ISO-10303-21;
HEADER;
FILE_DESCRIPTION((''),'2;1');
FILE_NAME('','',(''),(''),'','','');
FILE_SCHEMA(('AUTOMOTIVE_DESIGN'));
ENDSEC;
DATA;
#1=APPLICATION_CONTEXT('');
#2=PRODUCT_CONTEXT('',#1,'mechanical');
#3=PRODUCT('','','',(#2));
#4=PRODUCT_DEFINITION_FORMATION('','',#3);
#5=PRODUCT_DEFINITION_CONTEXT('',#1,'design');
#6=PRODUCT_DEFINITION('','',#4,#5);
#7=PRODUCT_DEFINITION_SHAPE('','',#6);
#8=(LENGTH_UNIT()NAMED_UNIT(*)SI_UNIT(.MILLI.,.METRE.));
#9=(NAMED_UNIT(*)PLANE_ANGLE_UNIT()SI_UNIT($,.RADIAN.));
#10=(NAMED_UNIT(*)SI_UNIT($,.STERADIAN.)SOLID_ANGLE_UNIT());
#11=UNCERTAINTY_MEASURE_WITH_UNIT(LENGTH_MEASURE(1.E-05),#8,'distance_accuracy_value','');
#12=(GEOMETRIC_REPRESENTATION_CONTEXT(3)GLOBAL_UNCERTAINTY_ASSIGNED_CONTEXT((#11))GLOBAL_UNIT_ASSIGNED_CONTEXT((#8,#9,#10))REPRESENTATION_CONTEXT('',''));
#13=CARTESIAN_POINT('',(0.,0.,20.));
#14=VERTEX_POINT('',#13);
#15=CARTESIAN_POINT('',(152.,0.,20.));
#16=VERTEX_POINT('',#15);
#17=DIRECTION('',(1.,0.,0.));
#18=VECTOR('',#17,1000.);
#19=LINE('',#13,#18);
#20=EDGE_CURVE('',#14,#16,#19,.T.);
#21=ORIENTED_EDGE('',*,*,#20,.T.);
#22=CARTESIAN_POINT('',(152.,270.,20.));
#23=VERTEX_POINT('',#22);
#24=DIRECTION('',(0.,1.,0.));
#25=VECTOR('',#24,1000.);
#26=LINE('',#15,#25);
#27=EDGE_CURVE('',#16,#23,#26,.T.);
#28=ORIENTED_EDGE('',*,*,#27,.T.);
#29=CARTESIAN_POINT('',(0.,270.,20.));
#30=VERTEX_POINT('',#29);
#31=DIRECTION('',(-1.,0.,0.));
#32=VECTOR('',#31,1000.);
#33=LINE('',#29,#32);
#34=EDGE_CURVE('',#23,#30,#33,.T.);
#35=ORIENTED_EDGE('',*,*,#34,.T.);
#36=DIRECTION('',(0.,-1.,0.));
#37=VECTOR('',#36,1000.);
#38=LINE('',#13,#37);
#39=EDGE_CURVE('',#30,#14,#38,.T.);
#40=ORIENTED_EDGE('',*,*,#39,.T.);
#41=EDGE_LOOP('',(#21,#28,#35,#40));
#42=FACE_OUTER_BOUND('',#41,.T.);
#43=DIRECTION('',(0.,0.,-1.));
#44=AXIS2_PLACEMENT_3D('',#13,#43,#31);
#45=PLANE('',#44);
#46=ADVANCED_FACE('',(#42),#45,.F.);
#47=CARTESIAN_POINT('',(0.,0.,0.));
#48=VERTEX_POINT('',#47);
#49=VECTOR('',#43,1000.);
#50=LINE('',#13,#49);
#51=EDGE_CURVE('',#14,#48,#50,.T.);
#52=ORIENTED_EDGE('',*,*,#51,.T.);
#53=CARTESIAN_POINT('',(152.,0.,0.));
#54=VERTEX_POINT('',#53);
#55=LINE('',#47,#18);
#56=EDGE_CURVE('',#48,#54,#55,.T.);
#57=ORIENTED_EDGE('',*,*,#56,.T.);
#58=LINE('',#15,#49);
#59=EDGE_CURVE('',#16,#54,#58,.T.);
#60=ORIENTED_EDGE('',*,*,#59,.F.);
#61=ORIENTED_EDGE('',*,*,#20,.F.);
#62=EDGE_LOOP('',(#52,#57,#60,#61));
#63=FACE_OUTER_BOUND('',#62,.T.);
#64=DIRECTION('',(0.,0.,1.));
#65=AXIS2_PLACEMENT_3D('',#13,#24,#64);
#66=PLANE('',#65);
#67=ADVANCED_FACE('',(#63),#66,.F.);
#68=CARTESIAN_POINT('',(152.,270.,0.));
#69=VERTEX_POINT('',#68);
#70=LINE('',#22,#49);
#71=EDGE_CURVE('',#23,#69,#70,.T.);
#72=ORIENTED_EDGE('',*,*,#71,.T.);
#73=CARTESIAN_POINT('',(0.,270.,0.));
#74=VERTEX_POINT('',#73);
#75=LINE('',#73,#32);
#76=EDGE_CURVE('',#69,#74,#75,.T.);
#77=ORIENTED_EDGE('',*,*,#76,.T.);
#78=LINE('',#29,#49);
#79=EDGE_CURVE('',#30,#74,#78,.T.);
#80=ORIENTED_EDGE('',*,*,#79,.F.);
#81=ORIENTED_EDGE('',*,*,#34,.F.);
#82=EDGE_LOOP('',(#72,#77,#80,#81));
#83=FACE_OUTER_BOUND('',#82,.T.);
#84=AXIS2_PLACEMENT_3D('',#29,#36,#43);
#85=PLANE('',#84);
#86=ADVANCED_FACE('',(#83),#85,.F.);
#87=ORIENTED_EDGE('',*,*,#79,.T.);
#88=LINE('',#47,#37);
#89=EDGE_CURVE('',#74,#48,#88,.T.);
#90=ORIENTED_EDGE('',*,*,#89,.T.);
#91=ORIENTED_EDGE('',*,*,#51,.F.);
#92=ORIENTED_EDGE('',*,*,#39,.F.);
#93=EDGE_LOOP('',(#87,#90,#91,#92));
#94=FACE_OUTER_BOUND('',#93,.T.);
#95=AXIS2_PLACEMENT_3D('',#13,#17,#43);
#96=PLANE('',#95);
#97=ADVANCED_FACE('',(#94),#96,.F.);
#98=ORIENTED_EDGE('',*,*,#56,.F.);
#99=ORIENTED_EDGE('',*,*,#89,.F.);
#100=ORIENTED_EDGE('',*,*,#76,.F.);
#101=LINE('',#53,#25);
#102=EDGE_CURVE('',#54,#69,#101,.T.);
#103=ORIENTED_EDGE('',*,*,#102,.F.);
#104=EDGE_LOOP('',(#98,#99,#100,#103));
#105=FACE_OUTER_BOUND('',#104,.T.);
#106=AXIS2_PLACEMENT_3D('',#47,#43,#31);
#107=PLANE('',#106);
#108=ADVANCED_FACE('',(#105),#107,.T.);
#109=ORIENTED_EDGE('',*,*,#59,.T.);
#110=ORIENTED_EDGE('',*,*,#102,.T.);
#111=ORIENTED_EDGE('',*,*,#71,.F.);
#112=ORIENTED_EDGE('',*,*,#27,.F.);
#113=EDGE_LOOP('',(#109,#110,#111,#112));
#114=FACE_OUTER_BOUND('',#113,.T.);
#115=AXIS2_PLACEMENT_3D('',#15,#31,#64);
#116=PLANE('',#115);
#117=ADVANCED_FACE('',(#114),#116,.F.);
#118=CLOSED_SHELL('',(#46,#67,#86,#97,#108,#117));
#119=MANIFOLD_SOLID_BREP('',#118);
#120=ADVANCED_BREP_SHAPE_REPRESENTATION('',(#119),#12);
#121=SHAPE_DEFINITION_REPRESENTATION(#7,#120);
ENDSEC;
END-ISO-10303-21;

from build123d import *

# Parameters (mm, degrees)
SKETCH1_W           = 152
SKETCH1_H           = 270
BOSS_EXTRUDE1_DEPTH = 20


with BuildPart() as part:
    # Sketch1 → Boss-Extrude1 (new body)
    with BuildSketch(Plane.XY):
        with Locations((76, 135)):
            Rectangle(SKETCH1_W, SKETCH1_H)
    extrude(amount=BOSS_EXTRUDE1_DEPTH)


solid = part.part
